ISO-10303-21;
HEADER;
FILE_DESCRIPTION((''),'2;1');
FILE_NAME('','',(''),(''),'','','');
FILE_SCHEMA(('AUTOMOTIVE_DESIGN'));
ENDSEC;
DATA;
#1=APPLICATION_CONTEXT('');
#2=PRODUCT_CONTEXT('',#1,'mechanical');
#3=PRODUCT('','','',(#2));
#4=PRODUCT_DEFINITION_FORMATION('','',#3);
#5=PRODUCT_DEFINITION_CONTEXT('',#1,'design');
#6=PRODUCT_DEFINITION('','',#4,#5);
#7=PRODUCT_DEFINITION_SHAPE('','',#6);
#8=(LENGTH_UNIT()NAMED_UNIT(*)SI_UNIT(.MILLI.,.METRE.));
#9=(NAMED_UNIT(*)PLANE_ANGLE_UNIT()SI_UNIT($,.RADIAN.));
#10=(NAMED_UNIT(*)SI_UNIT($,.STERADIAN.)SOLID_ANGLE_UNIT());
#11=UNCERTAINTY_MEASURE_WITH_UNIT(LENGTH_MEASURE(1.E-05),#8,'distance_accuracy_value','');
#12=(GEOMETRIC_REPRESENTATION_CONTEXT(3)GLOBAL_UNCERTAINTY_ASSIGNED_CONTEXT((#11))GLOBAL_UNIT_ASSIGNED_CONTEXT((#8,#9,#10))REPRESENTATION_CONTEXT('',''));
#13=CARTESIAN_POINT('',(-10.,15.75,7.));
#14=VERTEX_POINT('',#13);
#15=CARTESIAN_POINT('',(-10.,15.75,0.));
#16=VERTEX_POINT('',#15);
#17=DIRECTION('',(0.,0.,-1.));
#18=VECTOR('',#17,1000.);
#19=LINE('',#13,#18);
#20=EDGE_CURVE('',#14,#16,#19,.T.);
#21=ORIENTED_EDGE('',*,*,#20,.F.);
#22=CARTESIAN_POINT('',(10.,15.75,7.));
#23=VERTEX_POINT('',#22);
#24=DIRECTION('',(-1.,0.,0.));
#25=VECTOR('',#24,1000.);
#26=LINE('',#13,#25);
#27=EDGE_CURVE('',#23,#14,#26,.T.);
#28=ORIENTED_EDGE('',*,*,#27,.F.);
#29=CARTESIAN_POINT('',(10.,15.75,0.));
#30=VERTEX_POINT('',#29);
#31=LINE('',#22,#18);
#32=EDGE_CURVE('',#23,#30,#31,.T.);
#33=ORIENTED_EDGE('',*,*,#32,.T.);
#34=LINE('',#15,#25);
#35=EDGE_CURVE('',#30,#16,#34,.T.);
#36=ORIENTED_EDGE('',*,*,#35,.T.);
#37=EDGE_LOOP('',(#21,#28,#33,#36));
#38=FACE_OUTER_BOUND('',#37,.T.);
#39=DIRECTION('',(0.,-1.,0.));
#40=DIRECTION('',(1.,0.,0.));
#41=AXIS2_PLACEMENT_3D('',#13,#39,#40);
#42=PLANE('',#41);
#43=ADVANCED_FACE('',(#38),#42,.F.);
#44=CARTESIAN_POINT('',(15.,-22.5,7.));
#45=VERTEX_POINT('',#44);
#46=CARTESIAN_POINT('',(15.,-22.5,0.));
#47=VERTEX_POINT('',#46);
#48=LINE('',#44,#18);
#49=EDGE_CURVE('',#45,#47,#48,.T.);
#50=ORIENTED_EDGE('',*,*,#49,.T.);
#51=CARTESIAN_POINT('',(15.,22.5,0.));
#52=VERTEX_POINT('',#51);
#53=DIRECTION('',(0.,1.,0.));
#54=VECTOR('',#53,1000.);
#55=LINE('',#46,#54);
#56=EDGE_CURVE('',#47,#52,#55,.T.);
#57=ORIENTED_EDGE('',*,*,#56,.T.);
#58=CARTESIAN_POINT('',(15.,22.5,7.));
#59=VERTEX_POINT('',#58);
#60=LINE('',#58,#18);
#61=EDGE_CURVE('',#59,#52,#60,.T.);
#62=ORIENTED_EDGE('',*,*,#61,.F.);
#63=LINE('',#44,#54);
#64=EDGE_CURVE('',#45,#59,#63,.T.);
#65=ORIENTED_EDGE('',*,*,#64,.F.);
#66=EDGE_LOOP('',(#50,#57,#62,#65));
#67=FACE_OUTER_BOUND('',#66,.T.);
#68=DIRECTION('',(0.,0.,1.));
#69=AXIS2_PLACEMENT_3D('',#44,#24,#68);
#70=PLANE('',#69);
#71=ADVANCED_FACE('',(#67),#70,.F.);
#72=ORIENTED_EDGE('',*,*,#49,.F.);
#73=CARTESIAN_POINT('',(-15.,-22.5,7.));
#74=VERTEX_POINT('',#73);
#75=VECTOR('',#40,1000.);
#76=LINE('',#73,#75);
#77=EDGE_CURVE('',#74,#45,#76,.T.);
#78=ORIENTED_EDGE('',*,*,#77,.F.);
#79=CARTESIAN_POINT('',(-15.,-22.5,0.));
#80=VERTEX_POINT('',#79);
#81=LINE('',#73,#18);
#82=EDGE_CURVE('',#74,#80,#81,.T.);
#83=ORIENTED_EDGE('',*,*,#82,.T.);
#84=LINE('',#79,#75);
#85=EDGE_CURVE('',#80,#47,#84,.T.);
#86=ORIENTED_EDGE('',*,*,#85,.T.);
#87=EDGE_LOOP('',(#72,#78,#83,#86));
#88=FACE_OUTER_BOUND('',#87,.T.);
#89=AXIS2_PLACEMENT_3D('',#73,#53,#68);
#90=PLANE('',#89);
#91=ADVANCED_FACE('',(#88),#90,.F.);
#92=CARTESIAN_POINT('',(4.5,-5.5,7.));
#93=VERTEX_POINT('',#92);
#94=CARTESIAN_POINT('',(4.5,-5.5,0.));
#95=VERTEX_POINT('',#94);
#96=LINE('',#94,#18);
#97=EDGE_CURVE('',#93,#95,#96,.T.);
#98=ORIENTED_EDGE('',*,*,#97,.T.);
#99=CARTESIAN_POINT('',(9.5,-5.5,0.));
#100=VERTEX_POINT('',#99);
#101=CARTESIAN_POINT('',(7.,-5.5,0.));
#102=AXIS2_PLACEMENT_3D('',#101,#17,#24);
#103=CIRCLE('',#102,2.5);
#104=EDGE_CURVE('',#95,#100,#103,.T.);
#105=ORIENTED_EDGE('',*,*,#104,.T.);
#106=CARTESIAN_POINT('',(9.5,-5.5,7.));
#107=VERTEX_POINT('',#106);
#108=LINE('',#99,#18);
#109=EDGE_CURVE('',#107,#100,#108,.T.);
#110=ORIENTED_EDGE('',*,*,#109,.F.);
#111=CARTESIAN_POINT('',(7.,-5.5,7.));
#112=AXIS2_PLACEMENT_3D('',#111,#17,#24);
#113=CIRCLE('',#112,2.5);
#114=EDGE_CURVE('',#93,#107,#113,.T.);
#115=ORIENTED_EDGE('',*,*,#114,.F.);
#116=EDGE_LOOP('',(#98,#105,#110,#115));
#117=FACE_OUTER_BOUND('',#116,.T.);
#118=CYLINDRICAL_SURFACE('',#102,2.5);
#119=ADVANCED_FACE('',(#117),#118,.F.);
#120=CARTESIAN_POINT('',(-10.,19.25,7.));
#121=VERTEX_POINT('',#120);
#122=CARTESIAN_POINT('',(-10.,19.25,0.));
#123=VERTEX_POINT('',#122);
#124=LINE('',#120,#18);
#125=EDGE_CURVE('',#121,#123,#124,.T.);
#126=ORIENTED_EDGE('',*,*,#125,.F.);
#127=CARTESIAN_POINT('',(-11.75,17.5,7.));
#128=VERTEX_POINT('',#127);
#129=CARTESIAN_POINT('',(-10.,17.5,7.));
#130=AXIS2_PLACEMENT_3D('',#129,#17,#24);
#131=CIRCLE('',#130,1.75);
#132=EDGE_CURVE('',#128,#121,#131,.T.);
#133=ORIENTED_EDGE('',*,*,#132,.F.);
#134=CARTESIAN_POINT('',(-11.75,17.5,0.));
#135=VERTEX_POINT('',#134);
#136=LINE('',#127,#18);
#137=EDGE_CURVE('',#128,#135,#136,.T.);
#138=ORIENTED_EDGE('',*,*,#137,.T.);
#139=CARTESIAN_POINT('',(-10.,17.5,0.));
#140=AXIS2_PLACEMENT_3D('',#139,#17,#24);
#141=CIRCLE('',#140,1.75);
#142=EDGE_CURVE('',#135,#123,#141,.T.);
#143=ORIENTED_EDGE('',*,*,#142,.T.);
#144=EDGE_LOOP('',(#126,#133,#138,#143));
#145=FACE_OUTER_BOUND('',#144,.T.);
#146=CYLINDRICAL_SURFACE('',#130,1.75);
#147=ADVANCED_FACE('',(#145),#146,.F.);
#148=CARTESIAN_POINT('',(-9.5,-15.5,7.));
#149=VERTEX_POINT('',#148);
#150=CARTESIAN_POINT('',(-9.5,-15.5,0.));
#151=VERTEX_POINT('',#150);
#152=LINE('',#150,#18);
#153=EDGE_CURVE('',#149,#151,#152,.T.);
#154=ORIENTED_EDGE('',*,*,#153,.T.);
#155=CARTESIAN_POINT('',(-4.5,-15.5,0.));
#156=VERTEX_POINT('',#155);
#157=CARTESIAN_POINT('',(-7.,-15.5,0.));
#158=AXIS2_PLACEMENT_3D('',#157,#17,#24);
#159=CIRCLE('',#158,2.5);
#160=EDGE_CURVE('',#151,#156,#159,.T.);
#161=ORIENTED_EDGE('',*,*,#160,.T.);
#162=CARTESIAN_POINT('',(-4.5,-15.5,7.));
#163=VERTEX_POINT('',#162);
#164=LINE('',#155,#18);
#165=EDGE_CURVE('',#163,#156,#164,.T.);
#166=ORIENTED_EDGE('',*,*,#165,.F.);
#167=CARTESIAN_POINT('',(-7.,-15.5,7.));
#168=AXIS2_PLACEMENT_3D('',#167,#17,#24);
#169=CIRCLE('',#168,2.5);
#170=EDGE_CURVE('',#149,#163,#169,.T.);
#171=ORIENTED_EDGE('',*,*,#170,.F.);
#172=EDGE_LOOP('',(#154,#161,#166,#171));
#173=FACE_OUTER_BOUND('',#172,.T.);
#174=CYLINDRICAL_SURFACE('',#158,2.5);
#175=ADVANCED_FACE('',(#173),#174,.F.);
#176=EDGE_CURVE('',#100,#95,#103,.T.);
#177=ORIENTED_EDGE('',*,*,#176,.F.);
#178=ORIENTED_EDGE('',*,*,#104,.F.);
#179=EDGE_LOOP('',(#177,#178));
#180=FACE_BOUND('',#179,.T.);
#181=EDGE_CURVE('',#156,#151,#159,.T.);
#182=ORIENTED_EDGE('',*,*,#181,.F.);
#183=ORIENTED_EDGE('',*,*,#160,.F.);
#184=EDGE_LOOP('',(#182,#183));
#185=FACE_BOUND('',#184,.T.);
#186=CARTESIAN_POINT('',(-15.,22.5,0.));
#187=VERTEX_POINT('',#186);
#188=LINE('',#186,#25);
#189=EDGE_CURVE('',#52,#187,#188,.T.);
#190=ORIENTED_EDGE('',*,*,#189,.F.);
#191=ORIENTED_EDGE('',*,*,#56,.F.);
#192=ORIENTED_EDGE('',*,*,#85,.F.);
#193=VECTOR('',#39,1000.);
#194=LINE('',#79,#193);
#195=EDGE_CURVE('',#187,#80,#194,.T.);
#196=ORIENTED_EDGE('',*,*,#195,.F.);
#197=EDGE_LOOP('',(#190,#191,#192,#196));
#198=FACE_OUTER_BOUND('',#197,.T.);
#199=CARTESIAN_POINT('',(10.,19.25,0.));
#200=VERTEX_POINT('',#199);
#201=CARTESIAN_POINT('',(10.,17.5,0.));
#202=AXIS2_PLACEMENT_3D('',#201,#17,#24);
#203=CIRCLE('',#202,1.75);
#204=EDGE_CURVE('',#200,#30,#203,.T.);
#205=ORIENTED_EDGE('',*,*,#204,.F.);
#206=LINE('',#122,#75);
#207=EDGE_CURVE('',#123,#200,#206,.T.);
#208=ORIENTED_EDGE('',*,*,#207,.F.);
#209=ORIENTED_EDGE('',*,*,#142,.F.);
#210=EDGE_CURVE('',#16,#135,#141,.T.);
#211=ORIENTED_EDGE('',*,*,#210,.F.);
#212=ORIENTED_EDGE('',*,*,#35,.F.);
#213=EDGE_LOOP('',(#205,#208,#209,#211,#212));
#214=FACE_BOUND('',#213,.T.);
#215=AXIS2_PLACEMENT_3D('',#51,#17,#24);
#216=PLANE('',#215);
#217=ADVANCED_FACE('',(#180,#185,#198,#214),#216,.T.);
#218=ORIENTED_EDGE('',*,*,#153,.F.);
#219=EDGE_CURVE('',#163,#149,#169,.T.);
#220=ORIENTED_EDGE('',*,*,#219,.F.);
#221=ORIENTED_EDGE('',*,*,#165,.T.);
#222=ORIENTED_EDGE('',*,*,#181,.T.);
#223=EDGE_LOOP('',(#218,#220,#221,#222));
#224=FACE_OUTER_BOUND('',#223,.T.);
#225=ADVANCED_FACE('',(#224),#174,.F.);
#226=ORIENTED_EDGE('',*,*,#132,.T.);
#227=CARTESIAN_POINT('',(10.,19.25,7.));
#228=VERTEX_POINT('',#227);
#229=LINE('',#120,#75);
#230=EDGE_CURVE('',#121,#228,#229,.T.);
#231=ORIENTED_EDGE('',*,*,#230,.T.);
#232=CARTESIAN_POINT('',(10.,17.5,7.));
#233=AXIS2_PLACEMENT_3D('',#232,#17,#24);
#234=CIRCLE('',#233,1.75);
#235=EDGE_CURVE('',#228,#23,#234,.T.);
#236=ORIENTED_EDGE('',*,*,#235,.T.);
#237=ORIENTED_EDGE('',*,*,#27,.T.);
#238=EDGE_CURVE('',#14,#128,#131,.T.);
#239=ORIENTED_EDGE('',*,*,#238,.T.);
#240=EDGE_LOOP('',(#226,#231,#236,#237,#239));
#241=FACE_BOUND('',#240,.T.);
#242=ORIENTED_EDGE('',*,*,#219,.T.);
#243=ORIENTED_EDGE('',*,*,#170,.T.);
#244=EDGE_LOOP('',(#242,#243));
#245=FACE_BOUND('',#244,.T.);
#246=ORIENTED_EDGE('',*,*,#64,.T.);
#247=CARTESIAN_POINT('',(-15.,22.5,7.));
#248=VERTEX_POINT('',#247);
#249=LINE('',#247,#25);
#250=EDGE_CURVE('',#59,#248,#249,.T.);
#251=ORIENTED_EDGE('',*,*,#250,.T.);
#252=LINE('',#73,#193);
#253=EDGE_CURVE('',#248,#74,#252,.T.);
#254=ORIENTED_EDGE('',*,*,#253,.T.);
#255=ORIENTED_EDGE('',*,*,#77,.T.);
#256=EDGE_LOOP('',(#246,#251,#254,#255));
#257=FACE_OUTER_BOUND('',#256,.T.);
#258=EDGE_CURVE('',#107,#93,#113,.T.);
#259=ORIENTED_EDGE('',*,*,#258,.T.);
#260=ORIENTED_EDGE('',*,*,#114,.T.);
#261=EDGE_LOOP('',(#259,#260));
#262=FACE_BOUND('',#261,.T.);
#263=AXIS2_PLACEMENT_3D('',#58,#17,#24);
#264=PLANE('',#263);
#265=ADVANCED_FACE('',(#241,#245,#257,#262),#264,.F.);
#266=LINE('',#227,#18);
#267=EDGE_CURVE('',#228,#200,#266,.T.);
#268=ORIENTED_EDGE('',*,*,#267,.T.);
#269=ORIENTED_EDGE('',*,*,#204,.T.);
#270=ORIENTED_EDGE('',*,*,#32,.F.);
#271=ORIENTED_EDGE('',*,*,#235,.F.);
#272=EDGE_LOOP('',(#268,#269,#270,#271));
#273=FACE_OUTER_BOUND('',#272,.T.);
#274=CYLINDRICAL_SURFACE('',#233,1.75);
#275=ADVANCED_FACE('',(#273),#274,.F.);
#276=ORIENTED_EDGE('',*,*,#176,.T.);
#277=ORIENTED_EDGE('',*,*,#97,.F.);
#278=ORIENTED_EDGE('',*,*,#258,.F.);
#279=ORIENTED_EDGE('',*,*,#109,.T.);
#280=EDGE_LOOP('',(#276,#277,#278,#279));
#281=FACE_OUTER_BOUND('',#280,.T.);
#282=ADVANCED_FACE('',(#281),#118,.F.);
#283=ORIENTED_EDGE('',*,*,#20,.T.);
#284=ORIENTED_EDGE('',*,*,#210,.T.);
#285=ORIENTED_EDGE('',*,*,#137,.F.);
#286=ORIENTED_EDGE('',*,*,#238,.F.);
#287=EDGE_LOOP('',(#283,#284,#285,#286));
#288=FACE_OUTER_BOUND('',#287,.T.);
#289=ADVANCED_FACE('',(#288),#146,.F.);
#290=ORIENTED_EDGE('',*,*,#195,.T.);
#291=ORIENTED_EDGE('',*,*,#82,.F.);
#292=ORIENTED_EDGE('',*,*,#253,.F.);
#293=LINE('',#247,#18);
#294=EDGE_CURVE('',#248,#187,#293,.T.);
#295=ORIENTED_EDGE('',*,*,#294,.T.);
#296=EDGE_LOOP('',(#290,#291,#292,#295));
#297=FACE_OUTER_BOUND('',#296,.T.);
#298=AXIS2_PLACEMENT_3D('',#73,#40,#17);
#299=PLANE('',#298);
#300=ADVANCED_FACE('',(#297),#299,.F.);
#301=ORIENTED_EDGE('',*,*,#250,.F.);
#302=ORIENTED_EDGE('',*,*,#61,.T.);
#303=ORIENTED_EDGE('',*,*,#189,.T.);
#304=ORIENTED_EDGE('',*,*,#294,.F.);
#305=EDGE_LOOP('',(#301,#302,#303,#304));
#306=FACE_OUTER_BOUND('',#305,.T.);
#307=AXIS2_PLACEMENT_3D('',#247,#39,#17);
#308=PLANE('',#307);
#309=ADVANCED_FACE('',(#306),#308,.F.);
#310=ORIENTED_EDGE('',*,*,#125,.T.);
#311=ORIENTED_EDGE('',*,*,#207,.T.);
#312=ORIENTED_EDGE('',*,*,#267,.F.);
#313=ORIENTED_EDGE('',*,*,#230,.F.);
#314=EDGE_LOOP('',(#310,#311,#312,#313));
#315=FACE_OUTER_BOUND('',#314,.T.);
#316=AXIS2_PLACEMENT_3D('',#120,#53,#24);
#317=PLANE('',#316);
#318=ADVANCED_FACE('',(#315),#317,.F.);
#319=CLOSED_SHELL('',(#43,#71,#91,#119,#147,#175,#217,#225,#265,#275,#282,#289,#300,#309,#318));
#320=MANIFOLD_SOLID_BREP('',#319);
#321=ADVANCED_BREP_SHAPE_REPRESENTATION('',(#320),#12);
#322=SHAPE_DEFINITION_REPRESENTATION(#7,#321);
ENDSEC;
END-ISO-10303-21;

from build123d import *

# Parameters (mm, degrees)
SKETCH_1_W           = 30
SKETCH_1_H           = 45
BOSS_EXTRUDE_1_DEPTH = 7
CUT_EXTRUDE_1_DEPTH  = 28.932955447
M6_TAPPED_HOLE_1_D   = 5


with BuildPart() as part:
    # Sketch 1 → Boss-Extrude 1 (new body)
    with BuildSketch(Plane.XY):
        Rectangle(SKETCH_1_W, SKETCH_1_H)
    extrude(amount=BOSS_EXTRUDE_1_DEPTH)

    # Sketch 2 → Cut-Extrude 1 (cut, through all)
    with BuildSketch(Plane(origin=(0, 0, 0), x_dir=(-1, 0, 0), z_dir=(0, 0, -1))):
        with BuildLine():
            Line((10, 15.75), (-10, 15.75))
            ThreePointArc((-10, 15.75), (-11.75, 17.5), (-10, 19.25))
            Line((-10, 19.25), (10, 19.25))
            ThreePointArc((10, 19.25), (11.75, 17.5), (10, 15.75))
        make_face()
    extrude(amount=-CUT_EXTRUDE_1_DEPTH, mode=Mode.SUBTRACT)

    # M6 Tapped Hole 1 (through all)
    with Locations(Plane(origin=(0, 0, 0), x_dir=(-1, 0, 0), z_dir=(0, 0, -1))):
        with Locations((7, -15.5), (-7, -5.5)):
            Hole(M6_TAPPED_HOLE_1_D / 2)


solid = part.part
